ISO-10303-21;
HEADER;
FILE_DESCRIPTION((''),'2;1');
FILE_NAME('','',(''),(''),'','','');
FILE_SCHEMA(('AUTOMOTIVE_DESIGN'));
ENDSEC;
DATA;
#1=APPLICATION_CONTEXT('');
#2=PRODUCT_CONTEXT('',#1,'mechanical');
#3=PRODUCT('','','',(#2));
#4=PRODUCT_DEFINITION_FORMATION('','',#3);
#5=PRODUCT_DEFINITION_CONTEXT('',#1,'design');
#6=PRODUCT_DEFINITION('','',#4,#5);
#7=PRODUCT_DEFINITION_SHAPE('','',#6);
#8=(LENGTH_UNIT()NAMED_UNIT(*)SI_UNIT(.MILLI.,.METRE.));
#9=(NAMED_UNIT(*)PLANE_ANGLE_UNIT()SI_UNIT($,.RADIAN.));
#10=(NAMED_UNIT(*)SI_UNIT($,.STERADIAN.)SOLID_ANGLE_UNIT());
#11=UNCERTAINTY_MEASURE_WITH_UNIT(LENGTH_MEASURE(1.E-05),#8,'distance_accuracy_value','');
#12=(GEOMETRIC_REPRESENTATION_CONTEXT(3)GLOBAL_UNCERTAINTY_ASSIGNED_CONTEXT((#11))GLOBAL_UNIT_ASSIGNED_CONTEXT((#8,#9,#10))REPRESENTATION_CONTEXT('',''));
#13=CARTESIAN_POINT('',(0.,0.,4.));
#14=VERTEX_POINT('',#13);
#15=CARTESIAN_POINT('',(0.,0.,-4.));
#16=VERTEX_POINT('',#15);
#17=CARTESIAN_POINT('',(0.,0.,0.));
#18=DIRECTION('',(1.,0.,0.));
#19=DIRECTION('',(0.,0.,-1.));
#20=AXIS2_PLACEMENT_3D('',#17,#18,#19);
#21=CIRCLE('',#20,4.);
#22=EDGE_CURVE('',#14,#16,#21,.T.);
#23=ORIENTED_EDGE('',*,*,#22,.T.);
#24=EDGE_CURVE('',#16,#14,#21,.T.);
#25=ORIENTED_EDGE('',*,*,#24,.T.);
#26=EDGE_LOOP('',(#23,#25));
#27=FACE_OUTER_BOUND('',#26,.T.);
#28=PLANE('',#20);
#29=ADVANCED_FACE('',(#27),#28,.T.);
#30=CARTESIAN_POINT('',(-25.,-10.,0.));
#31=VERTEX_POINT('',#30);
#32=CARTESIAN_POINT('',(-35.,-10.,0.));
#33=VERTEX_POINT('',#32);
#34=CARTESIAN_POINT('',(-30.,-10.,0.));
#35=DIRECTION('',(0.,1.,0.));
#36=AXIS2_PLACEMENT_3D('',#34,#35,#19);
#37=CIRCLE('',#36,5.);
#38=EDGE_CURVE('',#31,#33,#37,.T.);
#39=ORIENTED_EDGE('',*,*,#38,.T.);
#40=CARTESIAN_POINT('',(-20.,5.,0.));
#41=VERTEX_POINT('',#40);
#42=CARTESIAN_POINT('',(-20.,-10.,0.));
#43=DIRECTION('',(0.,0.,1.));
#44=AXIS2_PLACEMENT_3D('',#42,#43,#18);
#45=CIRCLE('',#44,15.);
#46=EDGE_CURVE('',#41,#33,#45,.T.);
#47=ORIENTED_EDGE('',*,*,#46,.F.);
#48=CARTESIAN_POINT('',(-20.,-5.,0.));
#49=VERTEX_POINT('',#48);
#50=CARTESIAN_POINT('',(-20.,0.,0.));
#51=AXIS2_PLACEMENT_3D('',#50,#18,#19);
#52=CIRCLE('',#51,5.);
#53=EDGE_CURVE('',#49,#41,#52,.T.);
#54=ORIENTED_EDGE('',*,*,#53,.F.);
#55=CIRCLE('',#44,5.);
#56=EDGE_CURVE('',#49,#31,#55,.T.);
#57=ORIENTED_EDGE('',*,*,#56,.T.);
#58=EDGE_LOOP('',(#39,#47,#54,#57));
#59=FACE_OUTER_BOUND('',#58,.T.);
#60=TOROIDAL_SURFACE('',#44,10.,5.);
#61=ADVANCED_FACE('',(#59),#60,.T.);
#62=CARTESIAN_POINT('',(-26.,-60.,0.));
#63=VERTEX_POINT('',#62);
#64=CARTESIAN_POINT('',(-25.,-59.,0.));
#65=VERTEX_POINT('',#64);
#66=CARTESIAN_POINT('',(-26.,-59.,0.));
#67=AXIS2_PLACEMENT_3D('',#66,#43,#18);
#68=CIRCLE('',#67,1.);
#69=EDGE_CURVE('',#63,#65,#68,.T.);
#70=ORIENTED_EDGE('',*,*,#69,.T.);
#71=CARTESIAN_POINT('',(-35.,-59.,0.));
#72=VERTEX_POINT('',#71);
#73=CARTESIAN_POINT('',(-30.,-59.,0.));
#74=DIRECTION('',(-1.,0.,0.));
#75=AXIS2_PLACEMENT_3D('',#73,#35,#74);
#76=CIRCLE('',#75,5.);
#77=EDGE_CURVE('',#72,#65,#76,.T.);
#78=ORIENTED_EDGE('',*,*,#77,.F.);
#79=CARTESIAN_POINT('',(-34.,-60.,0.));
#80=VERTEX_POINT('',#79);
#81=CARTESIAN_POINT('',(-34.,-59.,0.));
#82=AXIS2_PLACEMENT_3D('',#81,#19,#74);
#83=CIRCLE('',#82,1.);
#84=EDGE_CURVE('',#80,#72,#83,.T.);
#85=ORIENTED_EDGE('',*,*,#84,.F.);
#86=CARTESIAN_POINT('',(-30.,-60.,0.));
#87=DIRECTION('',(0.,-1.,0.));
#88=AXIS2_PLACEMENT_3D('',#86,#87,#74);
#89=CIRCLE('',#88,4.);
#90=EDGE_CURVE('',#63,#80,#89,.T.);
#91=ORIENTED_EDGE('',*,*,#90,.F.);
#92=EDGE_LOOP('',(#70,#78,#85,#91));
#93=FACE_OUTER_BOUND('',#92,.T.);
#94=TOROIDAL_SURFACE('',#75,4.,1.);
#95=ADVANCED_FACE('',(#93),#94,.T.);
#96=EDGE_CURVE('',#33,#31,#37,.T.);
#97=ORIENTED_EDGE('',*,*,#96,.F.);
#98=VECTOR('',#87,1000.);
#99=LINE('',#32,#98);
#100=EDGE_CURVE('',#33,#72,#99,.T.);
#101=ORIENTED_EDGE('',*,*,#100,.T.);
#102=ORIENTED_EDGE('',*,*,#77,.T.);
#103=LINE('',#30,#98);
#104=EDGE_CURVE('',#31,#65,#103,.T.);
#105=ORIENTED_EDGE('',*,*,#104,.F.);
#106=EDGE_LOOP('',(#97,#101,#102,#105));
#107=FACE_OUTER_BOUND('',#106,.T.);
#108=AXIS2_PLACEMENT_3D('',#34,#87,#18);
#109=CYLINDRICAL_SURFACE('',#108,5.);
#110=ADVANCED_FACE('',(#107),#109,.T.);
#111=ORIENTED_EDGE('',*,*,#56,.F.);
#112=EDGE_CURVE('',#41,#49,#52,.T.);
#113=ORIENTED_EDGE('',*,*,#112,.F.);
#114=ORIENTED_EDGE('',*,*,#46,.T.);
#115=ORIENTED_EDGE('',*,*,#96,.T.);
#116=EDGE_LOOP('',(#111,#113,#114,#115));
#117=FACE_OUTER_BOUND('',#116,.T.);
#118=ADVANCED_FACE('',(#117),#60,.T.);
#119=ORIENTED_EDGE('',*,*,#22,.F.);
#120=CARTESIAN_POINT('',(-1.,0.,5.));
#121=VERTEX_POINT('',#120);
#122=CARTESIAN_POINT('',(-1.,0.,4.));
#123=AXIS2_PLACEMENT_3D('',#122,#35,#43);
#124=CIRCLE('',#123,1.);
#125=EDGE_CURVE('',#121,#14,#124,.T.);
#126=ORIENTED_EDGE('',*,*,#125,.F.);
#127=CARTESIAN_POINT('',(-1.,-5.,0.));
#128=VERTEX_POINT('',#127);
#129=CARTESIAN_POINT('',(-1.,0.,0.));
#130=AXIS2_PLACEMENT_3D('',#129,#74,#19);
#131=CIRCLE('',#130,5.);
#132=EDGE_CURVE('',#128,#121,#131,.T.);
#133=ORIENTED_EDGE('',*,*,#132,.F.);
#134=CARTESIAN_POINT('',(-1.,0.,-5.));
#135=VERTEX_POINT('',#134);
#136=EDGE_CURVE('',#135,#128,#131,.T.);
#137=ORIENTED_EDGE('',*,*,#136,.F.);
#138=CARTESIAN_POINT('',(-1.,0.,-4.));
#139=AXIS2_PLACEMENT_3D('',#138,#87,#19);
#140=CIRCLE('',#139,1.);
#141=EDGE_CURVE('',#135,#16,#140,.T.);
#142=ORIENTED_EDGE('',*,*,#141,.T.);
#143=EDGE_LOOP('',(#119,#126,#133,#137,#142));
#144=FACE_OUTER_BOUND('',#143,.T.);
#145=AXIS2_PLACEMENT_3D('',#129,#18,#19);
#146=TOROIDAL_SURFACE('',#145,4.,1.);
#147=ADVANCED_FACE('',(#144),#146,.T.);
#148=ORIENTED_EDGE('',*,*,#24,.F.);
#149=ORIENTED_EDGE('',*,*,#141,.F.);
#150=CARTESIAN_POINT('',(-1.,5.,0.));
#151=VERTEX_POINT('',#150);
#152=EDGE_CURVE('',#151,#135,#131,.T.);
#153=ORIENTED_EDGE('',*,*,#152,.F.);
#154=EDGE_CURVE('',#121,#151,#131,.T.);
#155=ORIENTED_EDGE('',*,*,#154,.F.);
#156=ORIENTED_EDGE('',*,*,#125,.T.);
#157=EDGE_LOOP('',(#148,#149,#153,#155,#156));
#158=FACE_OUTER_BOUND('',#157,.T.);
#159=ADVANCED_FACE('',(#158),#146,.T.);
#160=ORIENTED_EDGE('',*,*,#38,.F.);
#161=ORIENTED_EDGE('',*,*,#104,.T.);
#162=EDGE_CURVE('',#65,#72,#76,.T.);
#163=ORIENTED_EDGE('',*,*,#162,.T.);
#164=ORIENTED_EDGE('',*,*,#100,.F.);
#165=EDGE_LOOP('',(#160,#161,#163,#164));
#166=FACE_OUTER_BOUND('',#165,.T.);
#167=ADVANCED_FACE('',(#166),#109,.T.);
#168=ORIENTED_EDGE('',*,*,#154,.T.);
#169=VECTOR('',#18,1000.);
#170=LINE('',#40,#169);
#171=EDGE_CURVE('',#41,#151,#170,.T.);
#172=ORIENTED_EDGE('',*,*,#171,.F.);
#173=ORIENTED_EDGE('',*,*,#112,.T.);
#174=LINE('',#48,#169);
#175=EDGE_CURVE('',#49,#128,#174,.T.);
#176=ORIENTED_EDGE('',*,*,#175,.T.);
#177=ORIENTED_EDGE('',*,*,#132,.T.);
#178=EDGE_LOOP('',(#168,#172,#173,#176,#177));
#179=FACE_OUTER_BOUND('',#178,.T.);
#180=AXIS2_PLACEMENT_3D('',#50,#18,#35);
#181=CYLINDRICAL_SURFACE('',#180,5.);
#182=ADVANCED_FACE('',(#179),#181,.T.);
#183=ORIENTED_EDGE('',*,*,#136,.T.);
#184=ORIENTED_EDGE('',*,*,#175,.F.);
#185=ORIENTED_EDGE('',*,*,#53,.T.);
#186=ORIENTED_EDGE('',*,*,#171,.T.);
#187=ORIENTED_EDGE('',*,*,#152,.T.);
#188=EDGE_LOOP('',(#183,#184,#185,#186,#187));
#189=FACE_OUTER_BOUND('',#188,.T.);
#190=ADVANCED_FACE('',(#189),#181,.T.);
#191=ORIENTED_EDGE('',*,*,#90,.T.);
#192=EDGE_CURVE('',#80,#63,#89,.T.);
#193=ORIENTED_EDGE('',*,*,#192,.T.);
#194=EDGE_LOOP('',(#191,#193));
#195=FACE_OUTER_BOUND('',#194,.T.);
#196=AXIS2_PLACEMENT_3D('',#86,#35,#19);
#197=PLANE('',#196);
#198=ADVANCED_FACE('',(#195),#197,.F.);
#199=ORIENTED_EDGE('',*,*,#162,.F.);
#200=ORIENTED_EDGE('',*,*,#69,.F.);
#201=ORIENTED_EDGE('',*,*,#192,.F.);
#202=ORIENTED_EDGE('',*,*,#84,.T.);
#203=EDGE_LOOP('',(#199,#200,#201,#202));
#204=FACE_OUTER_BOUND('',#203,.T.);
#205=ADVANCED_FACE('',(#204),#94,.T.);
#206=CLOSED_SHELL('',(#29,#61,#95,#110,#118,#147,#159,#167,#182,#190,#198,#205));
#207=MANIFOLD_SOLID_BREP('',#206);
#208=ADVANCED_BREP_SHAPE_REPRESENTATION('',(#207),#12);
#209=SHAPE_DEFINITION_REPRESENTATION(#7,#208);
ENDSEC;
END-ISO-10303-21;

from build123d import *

# Parameters (mm, degrees)
SKETCH_2_R = 5
FILLET_1_R = 1


with BuildPart() as part:
    # 扫描1: sweep along a path in 草图1
    with BuildLine(Plane.XY) as sweep_1_path:
        Line((0, 0), (-20, 0))
        ThreePointArc((-20, 0), (-27.071067812, -2.928932188), (-30, -10))
        Line((-30, -10), (-30, -60))
    # 草图2 → 扫描1 (sweep)
    with BuildSketch(Plane(origin=(0, 0, 0), x_dir=(0, 0, -1), z_dir=(1, 0, 0))):
        Circle(SKETCH_2_R)
    sweep(path=sweep_1_path.line)

    # 圆角1
    fillet_1_edges = [part.edges().sort_by_distance(p)[0] for p in [
        (0, 0, 5),
        (-30, -60, 5),
    ]]
    fillet(fillet_1_edges, radius=FILLET_1_R)


solid = part.part
